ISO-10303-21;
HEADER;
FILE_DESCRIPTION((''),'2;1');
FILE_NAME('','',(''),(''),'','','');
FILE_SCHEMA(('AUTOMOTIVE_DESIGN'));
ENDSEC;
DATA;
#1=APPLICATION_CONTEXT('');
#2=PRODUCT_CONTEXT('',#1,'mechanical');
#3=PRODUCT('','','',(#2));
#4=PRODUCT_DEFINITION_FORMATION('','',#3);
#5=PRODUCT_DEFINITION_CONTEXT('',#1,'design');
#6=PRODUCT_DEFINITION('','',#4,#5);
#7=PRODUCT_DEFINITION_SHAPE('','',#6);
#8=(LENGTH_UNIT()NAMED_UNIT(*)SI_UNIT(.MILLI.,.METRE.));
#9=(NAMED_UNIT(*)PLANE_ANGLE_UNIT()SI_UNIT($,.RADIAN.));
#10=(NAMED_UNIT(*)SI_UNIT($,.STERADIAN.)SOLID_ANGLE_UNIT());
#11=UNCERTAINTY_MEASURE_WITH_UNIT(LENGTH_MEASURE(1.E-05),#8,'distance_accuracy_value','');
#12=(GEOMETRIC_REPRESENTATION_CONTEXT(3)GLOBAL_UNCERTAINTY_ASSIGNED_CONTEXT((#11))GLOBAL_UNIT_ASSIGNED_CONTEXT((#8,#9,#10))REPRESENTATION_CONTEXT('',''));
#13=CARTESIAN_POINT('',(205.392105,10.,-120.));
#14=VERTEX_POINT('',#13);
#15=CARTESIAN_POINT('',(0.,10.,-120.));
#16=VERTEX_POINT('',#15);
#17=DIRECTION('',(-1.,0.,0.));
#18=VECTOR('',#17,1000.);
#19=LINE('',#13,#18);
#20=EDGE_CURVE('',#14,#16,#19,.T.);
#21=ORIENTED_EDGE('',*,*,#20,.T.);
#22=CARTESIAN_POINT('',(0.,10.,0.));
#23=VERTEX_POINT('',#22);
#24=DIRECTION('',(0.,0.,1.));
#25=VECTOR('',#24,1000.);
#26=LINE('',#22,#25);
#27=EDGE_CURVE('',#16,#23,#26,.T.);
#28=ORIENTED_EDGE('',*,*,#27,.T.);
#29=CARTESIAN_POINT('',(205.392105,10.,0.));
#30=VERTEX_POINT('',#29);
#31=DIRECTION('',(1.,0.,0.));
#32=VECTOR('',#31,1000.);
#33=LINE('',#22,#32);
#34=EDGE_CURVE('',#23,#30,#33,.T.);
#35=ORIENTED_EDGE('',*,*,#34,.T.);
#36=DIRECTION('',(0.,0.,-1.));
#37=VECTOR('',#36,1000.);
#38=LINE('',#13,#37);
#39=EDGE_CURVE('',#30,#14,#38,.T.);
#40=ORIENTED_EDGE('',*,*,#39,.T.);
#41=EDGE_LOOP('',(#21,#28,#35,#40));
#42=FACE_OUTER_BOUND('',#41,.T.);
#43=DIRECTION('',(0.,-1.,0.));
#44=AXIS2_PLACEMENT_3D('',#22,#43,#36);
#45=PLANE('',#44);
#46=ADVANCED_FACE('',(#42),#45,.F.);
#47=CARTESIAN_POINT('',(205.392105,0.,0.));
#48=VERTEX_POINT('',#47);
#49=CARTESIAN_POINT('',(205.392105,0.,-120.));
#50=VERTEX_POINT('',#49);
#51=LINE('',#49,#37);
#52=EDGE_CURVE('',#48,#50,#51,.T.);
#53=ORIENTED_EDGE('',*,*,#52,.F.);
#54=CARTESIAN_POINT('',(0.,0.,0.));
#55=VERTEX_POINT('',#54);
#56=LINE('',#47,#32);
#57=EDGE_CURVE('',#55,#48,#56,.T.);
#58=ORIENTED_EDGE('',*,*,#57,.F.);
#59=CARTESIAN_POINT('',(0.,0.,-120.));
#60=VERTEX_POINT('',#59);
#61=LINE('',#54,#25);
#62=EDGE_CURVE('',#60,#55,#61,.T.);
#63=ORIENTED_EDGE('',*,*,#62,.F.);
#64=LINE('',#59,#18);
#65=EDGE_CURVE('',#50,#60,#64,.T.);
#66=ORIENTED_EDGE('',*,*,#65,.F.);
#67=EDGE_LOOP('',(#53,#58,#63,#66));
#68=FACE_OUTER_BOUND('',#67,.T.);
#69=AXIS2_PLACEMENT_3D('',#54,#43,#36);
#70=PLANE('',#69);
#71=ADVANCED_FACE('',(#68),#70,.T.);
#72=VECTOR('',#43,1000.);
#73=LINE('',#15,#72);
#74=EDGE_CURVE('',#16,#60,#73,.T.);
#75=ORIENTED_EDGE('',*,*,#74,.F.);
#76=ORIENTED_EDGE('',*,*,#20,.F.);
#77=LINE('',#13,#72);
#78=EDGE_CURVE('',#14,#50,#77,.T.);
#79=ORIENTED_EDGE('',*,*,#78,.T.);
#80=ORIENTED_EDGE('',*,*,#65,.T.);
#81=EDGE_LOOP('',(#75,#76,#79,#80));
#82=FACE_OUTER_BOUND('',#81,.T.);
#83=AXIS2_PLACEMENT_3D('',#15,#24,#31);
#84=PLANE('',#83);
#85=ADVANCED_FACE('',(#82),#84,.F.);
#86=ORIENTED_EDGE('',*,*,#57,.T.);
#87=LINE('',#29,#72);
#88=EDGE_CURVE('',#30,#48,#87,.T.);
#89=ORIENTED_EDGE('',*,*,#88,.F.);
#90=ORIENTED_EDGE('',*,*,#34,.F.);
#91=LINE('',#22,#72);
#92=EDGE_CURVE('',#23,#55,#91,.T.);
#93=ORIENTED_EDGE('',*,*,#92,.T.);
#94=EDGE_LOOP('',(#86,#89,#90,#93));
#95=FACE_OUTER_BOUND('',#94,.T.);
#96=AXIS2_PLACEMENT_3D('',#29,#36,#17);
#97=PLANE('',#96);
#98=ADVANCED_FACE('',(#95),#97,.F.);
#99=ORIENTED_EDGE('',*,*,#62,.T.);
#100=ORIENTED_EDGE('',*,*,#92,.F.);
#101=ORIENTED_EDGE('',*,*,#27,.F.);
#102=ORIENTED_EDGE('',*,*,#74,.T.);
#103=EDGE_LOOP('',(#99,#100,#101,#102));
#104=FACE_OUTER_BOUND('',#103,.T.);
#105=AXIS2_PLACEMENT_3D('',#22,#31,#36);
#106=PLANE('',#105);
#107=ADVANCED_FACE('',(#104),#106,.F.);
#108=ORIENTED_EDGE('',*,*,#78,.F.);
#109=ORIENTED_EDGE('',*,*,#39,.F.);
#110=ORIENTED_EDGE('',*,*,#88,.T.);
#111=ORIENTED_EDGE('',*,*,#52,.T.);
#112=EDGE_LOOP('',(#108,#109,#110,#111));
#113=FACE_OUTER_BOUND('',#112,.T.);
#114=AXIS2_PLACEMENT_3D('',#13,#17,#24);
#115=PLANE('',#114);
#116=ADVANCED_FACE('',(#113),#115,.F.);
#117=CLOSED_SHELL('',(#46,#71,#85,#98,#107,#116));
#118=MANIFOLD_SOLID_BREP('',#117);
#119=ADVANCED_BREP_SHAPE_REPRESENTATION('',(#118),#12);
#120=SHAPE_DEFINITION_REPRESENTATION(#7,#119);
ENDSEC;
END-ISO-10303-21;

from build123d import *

# Parameters (mm, degrees)
BOSS_EXTRUDE1_DEPTH = 10


with BuildPart() as part:
    # Sketch1 → Boss-Extrude1 (new body)
    with BuildSketch(Plane(origin=(0, 0, 0), x_dir=(1, 0, 0), z_dir=(0, 1, 0))):
        Polygon((205.392105032, 120), (205.392105032, 0), (200, 0), (0, 0), (0, 120), (200, 120), align=None)
    extrude(amount=BOSS_EXTRUDE1_DEPTH)


solid = part.part
